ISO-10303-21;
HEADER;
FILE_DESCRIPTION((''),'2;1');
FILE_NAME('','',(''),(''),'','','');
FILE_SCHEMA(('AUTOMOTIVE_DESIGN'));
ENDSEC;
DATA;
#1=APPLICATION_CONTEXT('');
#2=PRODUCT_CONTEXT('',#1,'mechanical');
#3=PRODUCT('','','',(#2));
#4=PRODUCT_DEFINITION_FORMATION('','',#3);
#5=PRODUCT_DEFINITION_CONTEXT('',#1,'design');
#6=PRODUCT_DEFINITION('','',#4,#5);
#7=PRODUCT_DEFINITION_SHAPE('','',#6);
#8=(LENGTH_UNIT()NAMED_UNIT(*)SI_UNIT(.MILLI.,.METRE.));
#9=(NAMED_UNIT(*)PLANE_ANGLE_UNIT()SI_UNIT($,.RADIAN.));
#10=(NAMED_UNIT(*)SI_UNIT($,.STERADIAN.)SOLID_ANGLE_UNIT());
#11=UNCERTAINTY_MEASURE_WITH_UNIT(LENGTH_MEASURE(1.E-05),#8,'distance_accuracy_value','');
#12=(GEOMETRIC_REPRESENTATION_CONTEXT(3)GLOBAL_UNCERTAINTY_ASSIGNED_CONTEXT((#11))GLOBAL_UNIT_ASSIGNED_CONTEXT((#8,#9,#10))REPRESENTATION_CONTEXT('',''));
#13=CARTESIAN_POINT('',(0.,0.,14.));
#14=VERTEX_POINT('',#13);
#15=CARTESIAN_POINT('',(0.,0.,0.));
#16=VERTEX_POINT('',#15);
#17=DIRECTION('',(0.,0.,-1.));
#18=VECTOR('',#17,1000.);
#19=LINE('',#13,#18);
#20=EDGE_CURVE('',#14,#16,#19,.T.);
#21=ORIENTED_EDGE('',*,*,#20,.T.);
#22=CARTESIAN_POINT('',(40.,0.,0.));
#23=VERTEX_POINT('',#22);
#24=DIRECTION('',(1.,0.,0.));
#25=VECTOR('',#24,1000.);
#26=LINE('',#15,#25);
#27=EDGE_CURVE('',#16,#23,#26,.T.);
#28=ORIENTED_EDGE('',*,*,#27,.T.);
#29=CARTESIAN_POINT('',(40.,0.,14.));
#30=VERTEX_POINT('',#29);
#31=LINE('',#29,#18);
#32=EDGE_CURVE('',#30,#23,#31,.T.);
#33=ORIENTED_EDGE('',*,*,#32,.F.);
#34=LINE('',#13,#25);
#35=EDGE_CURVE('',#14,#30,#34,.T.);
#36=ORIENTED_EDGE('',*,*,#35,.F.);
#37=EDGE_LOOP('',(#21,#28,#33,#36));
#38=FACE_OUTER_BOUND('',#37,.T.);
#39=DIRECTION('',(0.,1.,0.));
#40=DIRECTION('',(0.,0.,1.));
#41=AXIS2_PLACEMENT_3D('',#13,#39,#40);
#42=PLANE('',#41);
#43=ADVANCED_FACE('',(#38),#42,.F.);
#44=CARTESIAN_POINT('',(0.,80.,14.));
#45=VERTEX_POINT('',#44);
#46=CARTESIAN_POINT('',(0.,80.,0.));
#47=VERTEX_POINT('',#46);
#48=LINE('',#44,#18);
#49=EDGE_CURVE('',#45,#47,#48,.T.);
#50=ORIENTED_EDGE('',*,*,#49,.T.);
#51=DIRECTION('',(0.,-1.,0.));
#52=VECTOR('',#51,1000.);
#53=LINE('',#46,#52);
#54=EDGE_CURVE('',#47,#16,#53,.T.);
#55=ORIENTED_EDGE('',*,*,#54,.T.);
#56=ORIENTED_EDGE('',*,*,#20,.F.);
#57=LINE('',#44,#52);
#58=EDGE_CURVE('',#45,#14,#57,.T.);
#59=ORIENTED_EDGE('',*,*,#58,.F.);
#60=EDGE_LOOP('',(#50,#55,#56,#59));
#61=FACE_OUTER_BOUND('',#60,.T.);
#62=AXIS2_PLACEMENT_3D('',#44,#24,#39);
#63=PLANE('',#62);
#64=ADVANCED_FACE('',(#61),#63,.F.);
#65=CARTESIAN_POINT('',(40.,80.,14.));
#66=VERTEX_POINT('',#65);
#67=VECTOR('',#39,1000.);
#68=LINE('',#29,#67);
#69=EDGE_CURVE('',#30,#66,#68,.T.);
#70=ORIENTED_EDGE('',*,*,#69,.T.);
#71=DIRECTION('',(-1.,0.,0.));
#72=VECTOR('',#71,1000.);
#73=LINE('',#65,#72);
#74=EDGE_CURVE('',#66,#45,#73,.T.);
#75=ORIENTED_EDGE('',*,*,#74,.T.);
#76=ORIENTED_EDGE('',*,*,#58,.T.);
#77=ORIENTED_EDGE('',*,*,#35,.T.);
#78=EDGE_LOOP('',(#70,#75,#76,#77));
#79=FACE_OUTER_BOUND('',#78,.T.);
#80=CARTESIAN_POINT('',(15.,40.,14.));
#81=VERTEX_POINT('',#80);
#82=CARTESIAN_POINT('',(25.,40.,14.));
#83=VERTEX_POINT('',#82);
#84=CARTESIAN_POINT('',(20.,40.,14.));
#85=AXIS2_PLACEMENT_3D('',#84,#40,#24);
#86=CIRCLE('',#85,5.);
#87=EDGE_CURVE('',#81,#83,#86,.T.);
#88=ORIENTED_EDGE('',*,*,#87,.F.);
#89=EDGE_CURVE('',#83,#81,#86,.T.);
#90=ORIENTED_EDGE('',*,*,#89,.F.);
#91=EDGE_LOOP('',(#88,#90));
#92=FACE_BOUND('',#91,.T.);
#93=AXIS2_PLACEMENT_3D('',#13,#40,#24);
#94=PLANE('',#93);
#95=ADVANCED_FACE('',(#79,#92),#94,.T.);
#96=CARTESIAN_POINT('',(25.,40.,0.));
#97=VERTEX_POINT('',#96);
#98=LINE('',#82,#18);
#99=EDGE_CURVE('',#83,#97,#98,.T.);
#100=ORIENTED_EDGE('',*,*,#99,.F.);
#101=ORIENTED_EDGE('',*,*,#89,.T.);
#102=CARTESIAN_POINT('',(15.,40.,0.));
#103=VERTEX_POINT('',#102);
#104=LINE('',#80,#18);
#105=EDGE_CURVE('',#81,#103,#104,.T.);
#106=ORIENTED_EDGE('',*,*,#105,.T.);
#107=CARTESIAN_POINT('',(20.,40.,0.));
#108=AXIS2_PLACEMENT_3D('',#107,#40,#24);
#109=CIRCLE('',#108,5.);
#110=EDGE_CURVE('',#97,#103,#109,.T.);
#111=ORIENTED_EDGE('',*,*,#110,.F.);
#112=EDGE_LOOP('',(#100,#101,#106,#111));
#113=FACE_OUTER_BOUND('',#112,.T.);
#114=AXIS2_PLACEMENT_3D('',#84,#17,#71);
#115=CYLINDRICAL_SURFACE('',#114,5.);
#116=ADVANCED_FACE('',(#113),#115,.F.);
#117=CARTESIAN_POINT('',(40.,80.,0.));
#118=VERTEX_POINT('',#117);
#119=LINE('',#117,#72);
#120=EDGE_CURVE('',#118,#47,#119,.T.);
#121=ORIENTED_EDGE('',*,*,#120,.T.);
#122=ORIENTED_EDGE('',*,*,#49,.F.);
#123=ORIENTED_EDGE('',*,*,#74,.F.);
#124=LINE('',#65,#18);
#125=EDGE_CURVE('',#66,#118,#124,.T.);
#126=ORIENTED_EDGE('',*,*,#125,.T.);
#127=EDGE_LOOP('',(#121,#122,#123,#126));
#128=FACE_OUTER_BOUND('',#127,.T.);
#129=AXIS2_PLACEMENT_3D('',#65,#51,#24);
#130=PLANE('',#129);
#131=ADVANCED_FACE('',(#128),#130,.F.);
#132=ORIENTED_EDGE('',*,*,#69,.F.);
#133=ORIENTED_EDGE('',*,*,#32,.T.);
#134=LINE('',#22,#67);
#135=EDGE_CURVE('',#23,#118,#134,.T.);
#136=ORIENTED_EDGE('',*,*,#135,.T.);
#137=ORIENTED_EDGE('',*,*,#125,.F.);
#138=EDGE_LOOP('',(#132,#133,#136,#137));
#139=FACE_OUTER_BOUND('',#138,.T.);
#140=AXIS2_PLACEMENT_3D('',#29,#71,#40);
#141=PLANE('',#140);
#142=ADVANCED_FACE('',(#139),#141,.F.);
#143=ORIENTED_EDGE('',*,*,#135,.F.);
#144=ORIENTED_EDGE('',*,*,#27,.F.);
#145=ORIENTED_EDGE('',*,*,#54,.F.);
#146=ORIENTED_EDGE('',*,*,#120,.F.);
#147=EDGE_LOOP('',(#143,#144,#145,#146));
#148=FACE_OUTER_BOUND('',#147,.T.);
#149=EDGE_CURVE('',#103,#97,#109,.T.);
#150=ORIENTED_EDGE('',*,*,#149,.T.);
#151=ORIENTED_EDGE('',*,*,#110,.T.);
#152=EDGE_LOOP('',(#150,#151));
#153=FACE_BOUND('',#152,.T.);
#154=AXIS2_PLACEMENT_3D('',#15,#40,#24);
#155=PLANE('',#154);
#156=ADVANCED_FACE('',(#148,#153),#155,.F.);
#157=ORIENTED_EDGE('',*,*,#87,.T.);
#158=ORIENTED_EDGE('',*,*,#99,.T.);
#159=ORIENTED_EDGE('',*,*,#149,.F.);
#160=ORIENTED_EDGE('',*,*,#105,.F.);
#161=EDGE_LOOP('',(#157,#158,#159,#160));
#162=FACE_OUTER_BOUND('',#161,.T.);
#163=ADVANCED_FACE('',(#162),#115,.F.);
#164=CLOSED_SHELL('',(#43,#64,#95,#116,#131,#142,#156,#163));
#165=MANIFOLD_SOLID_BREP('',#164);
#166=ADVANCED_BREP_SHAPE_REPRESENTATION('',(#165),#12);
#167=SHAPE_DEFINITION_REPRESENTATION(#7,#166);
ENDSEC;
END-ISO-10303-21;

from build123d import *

# Parameters (mm, degrees)
SKETCH1_W           = 40
SKETCH1_H           = 80
SKETCH1_R           = 5
BOSS_EXTRUDE1_DEPTH = 14


with BuildPart() as part:
    # Sketch1 → Boss-Extrude1 (new body)
    with BuildSketch(Plane.XY):
        with Locations((20, 40)):
            Rectangle(SKETCH1_W, SKETCH1_H)
        with Locations((20, 40)):
            Circle(SKETCH1_R, mode=Mode.SUBTRACT)
    extrude(amount=BOSS_EXTRUDE1_DEPTH)


solid = part.part
